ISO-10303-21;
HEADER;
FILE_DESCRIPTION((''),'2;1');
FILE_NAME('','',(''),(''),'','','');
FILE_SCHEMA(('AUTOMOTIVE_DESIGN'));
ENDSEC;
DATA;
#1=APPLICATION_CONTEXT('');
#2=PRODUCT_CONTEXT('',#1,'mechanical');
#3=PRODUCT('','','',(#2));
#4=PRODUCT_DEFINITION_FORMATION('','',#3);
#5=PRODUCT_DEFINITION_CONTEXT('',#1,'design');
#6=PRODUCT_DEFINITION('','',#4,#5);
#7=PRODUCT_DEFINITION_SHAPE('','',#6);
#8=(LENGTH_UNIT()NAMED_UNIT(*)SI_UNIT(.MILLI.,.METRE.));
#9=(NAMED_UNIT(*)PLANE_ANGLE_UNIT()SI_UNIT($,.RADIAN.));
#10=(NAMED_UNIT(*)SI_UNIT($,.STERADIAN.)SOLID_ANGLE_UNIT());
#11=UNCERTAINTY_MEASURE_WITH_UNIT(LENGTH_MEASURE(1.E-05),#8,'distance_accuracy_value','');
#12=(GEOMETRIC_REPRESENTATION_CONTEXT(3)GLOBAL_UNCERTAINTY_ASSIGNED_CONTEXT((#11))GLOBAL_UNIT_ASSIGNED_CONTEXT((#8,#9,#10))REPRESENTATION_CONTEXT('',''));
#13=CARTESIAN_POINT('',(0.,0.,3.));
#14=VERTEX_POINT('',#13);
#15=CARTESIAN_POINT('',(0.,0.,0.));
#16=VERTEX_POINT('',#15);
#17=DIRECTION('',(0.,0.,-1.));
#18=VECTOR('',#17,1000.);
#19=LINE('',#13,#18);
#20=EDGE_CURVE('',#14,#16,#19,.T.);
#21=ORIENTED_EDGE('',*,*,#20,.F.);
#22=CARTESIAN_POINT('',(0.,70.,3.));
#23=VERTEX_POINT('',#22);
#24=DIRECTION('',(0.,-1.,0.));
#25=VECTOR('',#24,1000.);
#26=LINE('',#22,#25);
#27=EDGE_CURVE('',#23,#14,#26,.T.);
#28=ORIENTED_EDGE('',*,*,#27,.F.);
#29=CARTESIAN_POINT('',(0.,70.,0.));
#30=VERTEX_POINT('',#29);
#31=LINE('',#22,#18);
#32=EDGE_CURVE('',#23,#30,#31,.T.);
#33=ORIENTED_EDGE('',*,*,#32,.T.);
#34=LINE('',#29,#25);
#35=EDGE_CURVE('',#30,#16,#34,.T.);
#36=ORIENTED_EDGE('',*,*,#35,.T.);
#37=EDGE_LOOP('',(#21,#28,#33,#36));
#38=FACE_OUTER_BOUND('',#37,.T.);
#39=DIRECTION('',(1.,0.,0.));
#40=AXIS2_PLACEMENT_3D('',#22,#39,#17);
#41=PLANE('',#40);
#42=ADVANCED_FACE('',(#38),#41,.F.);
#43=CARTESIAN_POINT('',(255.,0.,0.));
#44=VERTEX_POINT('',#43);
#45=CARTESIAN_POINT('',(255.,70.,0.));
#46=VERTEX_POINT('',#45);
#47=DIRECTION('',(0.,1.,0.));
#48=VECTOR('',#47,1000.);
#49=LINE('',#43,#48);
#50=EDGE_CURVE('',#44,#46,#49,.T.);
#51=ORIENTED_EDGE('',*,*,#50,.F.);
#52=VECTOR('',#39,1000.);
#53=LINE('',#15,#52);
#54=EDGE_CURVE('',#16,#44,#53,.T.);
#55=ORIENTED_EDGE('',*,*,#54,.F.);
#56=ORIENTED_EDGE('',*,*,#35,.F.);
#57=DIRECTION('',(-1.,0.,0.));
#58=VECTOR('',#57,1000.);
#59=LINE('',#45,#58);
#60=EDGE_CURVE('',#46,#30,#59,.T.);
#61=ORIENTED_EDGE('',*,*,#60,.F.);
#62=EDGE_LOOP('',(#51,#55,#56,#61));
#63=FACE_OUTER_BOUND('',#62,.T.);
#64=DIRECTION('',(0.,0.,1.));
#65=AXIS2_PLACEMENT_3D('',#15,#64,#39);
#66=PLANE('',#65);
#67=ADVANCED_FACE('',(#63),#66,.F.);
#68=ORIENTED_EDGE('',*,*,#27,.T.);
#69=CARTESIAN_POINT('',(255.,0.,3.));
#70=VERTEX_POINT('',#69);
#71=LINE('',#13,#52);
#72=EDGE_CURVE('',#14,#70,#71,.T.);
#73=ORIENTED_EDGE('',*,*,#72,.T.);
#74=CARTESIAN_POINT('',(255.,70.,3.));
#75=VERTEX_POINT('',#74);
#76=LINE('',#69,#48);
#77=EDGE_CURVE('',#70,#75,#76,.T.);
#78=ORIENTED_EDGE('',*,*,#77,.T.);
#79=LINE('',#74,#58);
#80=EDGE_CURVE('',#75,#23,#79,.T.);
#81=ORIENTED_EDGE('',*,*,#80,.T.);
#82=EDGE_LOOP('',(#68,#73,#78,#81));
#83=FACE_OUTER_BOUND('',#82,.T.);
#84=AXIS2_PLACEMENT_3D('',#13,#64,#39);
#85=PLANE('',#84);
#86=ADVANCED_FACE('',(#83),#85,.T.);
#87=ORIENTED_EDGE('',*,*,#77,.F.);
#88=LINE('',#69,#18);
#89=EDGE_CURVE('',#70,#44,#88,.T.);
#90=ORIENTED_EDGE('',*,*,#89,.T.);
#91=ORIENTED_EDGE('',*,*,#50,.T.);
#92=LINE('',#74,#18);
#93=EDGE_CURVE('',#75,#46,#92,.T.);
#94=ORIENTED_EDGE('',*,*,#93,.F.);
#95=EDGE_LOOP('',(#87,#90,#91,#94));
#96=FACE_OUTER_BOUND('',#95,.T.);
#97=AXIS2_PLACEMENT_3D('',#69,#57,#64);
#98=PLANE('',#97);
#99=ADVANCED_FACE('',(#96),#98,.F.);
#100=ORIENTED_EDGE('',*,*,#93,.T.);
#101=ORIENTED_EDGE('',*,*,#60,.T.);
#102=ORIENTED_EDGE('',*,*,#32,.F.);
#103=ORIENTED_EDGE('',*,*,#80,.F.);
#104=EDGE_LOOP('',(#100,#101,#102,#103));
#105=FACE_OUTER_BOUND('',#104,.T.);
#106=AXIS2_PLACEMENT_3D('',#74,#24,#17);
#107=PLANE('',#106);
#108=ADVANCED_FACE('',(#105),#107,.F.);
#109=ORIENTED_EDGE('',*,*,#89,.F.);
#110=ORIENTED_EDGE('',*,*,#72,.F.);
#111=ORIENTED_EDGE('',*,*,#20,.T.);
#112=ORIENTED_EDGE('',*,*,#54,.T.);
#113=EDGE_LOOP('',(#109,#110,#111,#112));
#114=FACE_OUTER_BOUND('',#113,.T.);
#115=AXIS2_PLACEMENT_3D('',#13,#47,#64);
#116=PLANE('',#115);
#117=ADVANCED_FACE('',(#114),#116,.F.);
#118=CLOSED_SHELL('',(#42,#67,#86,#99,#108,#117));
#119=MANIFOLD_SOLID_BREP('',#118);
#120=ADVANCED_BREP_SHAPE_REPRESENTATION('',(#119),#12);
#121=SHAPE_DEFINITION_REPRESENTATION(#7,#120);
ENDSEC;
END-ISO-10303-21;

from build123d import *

# Parameters (mm, degrees)
SKETCH_1_W      = 255
SKETCH_1_H      = 70
EXTRUDE_1_DEPTH = 3


with BuildPart() as part:
    # 草图1 → 凸台-拉伸1 (new body)
    with BuildSketch(Plane.XY):
        with Locations((127.5, 35)):
            Rectangle(SKETCH_1_W, SKETCH_1_H)
    extrude(amount=EXTRUDE_1_DEPTH)


solid = part.part
